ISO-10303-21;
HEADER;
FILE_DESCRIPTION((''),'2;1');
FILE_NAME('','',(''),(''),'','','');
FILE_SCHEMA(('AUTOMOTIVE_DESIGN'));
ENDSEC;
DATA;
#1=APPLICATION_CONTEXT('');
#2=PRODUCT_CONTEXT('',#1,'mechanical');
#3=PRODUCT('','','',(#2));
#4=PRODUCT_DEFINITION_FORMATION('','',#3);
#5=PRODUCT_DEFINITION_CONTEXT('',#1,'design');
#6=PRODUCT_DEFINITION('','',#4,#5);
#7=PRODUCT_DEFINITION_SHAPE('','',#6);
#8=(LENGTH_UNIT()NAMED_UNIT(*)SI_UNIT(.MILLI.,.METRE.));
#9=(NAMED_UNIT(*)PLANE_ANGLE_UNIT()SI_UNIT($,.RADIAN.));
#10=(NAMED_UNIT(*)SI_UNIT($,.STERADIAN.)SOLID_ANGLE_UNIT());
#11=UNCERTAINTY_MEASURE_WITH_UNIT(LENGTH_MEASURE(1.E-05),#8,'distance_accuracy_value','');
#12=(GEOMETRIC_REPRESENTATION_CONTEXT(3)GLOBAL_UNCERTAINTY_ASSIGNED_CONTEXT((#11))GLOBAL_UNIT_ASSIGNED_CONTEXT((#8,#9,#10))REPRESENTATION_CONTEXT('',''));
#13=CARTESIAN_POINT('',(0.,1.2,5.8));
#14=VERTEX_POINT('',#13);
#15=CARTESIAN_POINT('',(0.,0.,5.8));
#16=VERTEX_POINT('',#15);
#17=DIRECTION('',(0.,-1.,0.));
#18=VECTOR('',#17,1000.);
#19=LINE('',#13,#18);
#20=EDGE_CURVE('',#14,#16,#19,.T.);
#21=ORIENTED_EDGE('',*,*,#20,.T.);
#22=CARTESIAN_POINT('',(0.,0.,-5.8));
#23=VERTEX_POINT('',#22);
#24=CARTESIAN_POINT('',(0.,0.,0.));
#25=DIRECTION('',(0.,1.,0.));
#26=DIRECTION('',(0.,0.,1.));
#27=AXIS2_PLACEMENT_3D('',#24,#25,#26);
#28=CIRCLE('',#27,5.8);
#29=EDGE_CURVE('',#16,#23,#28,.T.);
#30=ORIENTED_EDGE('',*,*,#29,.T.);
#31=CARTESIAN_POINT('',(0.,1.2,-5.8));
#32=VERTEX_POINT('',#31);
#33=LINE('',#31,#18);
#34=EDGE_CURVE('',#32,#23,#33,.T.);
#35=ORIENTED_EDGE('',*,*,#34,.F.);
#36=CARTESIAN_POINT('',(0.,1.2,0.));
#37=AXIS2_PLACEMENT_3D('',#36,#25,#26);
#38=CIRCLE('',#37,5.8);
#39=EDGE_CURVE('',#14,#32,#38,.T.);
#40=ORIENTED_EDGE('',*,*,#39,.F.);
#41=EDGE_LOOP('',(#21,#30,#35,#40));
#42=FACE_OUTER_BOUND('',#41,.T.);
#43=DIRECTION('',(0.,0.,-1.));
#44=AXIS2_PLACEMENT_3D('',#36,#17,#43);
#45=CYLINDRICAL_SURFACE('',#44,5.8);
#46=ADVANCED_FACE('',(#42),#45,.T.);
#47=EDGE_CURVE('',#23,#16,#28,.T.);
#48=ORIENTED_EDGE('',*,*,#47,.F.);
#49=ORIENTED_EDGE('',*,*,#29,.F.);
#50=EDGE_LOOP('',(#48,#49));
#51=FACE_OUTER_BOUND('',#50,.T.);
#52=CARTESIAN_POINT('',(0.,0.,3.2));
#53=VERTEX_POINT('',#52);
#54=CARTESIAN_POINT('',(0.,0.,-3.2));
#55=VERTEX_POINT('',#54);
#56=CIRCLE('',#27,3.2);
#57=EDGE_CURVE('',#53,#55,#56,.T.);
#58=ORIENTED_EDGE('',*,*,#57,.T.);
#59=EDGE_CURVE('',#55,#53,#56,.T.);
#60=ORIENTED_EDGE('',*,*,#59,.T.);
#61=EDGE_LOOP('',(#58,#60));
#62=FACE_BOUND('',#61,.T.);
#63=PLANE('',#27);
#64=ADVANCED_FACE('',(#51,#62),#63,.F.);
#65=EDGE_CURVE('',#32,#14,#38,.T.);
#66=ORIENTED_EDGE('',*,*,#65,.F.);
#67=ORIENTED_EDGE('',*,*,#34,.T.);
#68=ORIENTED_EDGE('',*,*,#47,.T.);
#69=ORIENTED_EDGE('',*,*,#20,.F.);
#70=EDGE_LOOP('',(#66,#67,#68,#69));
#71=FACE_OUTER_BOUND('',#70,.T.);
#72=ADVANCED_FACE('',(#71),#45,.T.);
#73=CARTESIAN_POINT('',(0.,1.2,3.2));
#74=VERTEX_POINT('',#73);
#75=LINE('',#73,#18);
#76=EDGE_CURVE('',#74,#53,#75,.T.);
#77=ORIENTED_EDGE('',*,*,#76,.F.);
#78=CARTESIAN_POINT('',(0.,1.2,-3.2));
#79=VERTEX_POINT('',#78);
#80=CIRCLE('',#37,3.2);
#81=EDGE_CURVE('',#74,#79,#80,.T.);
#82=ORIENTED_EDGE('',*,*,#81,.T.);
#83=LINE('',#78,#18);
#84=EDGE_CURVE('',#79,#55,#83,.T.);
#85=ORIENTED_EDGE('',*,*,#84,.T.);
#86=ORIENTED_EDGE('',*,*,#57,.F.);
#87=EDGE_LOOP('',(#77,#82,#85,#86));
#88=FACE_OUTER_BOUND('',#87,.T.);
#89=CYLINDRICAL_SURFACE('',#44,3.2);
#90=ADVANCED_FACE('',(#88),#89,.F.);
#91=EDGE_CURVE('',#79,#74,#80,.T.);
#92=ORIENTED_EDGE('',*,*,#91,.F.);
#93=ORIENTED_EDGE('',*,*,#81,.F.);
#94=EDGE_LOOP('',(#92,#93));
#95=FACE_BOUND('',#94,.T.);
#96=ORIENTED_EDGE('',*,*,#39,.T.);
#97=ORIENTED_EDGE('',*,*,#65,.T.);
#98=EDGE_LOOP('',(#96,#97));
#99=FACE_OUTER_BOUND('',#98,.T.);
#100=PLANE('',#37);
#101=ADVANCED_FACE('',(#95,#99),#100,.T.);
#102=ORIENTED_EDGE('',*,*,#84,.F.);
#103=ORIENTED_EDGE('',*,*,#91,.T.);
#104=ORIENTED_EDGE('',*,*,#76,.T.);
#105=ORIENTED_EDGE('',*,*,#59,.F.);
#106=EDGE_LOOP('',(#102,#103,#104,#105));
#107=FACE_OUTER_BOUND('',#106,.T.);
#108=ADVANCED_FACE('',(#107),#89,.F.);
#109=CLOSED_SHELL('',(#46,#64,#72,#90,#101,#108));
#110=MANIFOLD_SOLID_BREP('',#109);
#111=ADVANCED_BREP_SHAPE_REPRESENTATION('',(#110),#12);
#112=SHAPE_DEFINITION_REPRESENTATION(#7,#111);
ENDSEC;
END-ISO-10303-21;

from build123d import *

# Parameters (mm, degrees)
SKETCH_1_R      = 5.8
SKETCH_1_R_2    = 3.2
EXTRUDE_1_DEPTH = 1.2


with BuildPart() as part:
    # 草图1 → 凸台-拉伸1 (new body)
    with BuildSketch(Plane(origin=(0, 0, 0), x_dir=(1, 0, 0), z_dir=(0, 1, 0))):
        with Locations(Location((0, 0, 0), (0, 0, 270))):
            Circle(SKETCH_1_R)
        with Locations(Location((0, 0, 0), (0, 0, 270))):
            Circle(SKETCH_1_R_2, mode=Mode.SUBTRACT)
    extrude(amount=EXTRUDE_1_DEPTH)


solid = part.part
